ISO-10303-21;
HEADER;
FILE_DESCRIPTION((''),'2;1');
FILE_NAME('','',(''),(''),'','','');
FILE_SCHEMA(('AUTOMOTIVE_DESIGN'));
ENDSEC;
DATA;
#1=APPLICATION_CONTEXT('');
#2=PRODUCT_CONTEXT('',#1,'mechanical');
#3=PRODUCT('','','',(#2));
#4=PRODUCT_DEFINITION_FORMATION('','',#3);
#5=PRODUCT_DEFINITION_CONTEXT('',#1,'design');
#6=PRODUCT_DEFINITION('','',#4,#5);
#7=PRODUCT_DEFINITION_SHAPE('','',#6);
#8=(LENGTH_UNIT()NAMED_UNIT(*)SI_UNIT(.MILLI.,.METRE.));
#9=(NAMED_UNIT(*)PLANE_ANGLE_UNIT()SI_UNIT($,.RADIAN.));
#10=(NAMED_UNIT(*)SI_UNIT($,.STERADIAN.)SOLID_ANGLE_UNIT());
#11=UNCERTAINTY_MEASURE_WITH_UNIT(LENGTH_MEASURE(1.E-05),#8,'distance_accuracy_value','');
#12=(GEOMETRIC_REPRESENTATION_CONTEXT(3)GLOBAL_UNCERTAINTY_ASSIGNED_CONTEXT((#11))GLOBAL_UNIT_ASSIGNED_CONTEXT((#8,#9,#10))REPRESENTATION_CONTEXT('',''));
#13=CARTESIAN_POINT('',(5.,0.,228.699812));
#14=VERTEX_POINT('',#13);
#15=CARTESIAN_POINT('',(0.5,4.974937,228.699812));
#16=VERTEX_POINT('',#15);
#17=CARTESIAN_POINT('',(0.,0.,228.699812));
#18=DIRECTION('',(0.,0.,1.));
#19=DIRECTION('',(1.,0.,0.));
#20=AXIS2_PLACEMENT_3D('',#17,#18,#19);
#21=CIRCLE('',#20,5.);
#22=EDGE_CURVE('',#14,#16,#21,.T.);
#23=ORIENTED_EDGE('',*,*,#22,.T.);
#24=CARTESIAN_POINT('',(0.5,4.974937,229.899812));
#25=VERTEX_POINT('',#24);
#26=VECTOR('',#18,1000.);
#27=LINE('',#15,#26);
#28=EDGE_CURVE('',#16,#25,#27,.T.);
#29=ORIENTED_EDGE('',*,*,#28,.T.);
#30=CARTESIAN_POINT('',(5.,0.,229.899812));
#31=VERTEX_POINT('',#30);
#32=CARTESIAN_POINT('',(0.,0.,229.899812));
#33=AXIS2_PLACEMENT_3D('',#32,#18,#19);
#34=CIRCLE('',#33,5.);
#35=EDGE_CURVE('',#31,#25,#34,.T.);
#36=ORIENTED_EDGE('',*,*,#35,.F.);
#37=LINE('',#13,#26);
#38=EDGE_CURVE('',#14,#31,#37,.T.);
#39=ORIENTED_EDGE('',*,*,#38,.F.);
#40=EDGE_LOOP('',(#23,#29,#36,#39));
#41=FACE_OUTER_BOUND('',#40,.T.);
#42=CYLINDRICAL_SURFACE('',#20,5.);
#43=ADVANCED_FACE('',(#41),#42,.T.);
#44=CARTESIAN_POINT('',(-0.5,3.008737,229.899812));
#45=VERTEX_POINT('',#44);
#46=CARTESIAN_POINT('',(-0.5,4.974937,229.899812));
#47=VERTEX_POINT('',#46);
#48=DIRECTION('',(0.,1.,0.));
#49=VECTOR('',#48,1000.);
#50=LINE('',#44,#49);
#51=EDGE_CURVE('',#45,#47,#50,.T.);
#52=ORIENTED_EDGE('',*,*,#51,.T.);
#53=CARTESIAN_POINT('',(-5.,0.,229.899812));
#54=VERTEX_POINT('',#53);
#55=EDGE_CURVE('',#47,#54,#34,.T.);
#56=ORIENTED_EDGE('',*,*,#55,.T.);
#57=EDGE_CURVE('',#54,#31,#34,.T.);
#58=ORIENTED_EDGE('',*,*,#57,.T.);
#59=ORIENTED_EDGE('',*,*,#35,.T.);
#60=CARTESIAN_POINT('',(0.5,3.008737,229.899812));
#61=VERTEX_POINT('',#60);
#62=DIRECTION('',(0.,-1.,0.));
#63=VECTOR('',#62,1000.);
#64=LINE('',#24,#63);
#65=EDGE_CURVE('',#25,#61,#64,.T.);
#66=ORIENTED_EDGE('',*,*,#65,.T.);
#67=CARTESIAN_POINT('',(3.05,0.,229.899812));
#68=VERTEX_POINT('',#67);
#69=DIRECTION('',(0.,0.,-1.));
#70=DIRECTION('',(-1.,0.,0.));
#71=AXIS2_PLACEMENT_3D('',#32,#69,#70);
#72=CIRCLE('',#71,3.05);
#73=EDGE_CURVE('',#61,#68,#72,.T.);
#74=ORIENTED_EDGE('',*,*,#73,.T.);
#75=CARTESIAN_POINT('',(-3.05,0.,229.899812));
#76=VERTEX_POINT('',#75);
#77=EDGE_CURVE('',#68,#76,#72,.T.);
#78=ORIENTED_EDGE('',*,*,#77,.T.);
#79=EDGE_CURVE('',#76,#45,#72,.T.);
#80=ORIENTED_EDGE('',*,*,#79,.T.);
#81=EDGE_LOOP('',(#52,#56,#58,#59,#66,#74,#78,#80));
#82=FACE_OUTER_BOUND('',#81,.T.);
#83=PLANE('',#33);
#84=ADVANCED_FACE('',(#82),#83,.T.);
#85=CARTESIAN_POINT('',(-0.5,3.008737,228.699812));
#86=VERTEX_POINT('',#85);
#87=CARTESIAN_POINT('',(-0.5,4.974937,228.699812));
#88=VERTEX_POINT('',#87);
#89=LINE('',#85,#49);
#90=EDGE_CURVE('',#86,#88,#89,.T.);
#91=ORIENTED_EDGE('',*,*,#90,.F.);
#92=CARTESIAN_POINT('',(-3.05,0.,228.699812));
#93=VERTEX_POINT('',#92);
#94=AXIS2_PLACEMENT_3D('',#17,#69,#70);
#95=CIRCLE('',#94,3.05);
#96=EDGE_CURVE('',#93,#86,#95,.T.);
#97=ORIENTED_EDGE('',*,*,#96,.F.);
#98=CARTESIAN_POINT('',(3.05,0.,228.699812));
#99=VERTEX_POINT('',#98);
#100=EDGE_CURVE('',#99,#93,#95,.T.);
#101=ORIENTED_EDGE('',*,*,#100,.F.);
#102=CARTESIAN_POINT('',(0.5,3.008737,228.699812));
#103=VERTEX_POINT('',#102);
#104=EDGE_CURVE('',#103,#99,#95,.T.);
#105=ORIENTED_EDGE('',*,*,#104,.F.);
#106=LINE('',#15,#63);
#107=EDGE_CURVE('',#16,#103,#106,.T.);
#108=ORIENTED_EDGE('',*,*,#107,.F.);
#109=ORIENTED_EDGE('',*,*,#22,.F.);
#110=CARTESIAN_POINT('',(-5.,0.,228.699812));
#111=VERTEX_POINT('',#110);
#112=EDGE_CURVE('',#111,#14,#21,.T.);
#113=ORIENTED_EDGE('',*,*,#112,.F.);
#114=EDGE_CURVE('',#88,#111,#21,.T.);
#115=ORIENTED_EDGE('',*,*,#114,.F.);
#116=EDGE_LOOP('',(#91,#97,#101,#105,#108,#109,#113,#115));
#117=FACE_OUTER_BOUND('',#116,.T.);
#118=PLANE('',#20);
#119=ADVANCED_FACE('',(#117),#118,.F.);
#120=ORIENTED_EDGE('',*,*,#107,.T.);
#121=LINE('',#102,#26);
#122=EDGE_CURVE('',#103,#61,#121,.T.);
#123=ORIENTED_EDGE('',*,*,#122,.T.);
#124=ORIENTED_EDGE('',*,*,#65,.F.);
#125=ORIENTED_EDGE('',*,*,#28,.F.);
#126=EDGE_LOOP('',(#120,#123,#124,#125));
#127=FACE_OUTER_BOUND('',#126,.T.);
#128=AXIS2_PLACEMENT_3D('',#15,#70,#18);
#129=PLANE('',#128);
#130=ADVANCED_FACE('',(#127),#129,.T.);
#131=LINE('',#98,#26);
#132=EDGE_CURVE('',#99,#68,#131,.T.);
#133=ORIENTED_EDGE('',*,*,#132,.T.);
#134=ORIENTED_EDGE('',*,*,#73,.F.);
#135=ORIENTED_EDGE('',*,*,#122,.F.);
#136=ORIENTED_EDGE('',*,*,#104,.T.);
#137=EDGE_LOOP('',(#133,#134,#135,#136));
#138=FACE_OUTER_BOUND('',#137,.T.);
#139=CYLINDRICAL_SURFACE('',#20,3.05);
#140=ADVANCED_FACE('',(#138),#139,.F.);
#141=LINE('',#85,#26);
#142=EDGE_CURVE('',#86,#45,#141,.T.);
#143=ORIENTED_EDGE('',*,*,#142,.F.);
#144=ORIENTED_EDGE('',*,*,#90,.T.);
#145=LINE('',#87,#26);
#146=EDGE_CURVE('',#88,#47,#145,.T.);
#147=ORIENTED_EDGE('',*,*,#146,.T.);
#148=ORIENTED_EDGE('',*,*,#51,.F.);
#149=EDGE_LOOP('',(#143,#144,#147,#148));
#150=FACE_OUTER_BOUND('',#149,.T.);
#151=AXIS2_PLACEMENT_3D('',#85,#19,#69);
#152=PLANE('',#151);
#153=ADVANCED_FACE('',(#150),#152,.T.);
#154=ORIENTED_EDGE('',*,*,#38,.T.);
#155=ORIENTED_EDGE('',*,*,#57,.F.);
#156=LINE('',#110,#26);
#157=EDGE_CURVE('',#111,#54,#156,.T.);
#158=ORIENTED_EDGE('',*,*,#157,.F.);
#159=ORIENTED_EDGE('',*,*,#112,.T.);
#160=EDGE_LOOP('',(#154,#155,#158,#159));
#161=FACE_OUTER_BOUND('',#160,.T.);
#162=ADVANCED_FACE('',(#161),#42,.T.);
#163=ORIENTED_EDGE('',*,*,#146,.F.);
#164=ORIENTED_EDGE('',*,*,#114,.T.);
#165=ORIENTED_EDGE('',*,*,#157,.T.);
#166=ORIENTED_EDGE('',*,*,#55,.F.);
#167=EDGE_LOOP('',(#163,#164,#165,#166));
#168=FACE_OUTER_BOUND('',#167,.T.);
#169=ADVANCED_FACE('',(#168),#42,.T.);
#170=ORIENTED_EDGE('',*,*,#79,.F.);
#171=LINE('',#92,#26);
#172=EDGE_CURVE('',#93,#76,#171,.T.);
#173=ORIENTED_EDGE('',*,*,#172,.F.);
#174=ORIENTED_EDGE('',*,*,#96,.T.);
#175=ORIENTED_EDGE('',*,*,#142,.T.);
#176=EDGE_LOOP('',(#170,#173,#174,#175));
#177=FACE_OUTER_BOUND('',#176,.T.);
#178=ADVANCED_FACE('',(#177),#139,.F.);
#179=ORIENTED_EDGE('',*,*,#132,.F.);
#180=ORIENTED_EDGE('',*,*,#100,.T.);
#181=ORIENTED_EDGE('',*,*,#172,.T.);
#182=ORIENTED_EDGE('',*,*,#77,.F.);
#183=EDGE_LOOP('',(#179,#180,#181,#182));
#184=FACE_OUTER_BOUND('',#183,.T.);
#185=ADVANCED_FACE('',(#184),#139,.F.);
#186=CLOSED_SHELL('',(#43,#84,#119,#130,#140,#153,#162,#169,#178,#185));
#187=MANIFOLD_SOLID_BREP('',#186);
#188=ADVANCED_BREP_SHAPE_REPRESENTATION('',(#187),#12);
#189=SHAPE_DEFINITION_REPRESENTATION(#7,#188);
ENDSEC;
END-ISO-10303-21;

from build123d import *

# Parameters (mm, degrees)
BOSS_EXTRUDE1_DEPTH = 1.2


with BuildPart() as part:
    # Sketch1 → Boss-Extrude1 (new body)
    with BuildSketch(Plane.XY.offset(229.899812353)):
        with BuildLine():
            Line((0.5, 4.974937186), (0.5, 3.008737277))
            ThreePointArc((0.5, 3.008737277), (0, -3.05), (-0.5, 3.008737277))
            Line((-0.5, 3.008737277), (-0.5, 4.974937186))
            ThreePointArc((-0.5, 4.974937186), (0, -5), (0.5, 4.974937186))
        make_face()
    extrude(amount=-BOSS_EXTRUDE1_DEPTH)


solid = part.part
